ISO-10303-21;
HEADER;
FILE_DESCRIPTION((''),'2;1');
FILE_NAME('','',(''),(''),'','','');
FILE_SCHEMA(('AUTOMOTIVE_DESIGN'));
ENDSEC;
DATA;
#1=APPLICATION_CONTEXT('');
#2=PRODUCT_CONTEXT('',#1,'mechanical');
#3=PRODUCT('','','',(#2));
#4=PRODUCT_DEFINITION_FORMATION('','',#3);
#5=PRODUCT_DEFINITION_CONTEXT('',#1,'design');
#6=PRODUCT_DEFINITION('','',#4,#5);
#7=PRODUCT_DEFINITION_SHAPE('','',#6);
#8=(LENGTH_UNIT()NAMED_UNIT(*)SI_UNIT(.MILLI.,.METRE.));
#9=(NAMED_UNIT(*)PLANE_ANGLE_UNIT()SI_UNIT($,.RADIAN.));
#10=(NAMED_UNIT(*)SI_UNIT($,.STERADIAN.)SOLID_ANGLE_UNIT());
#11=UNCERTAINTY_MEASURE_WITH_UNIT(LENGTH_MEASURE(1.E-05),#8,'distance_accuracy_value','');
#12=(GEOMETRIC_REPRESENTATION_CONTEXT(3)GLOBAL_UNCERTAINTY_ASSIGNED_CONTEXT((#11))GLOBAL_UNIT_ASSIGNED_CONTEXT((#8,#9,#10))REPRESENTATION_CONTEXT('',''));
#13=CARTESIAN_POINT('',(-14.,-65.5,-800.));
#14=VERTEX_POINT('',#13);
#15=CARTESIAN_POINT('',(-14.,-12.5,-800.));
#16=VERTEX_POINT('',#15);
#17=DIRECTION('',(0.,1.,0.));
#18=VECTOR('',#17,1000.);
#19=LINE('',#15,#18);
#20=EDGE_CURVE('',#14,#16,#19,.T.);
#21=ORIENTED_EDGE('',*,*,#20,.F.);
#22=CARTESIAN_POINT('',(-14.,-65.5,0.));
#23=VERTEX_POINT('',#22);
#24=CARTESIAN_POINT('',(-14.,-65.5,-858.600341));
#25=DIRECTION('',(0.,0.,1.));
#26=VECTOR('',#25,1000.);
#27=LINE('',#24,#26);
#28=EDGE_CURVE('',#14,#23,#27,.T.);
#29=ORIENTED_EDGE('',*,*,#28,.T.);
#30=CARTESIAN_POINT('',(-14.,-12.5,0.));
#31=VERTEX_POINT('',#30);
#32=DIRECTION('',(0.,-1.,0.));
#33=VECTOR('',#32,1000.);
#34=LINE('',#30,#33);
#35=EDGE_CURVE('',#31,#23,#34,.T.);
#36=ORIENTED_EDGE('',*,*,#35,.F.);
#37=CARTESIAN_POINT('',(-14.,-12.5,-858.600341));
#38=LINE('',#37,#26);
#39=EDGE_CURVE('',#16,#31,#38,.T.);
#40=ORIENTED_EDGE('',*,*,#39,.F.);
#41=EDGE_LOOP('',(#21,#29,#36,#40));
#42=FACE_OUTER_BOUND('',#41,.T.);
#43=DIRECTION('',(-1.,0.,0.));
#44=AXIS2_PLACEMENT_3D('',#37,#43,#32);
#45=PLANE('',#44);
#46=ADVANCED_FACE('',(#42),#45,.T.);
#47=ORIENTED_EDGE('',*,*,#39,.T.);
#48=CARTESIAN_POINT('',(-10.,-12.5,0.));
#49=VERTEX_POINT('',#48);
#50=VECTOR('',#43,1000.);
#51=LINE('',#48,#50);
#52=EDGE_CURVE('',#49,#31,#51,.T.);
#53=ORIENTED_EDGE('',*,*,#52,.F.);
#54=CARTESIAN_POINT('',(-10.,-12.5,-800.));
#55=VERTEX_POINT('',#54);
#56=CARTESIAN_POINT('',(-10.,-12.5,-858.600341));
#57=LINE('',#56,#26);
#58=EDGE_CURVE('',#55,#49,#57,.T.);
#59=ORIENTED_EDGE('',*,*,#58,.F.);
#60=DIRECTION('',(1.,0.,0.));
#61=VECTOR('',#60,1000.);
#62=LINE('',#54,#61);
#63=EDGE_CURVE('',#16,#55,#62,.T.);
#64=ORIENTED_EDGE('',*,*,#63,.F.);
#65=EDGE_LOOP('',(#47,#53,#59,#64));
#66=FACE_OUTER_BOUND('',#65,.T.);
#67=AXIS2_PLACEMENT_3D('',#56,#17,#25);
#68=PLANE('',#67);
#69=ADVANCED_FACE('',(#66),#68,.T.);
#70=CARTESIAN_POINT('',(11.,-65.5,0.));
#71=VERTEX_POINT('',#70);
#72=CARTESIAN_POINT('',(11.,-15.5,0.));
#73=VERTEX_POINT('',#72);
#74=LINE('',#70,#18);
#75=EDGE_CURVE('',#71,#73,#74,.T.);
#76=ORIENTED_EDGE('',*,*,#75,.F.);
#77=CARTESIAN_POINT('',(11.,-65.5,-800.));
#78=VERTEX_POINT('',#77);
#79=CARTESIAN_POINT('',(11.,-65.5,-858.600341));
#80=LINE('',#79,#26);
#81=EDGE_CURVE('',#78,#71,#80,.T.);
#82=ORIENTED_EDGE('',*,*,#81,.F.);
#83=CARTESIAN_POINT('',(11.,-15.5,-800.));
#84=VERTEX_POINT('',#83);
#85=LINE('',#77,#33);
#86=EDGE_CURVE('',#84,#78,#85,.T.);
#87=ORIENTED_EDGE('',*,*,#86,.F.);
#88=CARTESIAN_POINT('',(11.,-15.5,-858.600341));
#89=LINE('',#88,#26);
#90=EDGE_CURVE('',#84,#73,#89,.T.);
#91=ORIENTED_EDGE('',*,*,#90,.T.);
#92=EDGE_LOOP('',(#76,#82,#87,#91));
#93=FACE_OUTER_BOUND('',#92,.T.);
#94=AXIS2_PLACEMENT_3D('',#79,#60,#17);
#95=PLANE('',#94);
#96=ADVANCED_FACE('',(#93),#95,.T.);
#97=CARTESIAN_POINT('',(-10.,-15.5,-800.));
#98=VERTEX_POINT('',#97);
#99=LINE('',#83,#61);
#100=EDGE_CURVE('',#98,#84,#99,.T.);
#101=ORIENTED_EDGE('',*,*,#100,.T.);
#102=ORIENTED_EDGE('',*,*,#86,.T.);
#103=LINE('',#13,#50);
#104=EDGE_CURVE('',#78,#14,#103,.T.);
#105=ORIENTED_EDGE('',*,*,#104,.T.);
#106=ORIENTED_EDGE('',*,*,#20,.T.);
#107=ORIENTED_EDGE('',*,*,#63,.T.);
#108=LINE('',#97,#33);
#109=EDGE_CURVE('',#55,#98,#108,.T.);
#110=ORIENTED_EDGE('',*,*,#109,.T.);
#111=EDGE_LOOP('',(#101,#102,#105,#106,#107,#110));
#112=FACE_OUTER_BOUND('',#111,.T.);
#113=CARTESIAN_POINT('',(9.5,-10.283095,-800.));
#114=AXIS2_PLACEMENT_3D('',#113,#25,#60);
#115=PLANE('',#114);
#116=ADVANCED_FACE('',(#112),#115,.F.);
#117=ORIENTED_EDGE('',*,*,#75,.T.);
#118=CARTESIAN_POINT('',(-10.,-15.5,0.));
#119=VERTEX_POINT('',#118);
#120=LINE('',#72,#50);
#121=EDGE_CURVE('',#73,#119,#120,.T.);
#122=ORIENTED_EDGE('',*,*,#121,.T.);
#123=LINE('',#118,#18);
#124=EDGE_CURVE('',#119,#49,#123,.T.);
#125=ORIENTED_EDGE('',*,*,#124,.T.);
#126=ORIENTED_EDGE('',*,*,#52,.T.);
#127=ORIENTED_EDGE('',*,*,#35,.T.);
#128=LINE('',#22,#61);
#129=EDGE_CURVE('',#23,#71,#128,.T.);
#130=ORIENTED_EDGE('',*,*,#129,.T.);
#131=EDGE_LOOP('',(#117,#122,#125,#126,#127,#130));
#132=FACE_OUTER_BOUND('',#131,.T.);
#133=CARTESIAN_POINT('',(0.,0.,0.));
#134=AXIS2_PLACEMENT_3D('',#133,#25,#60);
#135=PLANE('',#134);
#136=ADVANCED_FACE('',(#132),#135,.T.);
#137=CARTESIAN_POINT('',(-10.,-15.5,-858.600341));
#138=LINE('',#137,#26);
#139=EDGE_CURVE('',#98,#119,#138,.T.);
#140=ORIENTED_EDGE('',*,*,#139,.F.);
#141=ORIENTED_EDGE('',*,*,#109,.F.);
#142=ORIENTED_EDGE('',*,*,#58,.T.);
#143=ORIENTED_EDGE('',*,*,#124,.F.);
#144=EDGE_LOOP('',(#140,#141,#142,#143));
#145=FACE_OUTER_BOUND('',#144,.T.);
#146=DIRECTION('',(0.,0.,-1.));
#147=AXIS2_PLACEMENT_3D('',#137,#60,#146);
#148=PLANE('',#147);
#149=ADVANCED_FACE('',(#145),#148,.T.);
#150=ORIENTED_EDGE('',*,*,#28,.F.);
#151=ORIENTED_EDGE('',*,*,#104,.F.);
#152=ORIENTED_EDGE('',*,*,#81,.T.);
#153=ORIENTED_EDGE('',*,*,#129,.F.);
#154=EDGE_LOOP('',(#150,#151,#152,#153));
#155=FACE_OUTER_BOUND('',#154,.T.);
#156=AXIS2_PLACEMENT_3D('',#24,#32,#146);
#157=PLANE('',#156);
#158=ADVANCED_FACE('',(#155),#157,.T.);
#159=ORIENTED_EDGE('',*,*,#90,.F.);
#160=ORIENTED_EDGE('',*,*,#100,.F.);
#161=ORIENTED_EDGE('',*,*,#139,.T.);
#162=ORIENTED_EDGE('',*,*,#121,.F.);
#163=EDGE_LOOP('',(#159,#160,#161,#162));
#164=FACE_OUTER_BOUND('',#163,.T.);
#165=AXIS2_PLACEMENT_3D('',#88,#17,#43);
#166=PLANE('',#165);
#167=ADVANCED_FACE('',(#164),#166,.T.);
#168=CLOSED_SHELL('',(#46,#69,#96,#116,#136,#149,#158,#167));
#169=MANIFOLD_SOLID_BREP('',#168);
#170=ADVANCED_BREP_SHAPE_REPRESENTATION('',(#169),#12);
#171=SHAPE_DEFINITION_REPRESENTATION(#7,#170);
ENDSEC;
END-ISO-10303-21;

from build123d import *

# Parameters (mm, degrees)
EXTRUDE_1_DEPTH = 800


with BuildPart() as part:
    # 草图1 → 凸台-拉伸1 (new body)
    with BuildSketch(Plane.XY):
        Polygon((-10, -12.5), (-14, -12.5), (-14, -65.5), (11, -65.5), (11, -15.5), (-10, -15.5), align=None)
    extrude(amount=-EXTRUDE_1_DEPTH)


solid = part.part
